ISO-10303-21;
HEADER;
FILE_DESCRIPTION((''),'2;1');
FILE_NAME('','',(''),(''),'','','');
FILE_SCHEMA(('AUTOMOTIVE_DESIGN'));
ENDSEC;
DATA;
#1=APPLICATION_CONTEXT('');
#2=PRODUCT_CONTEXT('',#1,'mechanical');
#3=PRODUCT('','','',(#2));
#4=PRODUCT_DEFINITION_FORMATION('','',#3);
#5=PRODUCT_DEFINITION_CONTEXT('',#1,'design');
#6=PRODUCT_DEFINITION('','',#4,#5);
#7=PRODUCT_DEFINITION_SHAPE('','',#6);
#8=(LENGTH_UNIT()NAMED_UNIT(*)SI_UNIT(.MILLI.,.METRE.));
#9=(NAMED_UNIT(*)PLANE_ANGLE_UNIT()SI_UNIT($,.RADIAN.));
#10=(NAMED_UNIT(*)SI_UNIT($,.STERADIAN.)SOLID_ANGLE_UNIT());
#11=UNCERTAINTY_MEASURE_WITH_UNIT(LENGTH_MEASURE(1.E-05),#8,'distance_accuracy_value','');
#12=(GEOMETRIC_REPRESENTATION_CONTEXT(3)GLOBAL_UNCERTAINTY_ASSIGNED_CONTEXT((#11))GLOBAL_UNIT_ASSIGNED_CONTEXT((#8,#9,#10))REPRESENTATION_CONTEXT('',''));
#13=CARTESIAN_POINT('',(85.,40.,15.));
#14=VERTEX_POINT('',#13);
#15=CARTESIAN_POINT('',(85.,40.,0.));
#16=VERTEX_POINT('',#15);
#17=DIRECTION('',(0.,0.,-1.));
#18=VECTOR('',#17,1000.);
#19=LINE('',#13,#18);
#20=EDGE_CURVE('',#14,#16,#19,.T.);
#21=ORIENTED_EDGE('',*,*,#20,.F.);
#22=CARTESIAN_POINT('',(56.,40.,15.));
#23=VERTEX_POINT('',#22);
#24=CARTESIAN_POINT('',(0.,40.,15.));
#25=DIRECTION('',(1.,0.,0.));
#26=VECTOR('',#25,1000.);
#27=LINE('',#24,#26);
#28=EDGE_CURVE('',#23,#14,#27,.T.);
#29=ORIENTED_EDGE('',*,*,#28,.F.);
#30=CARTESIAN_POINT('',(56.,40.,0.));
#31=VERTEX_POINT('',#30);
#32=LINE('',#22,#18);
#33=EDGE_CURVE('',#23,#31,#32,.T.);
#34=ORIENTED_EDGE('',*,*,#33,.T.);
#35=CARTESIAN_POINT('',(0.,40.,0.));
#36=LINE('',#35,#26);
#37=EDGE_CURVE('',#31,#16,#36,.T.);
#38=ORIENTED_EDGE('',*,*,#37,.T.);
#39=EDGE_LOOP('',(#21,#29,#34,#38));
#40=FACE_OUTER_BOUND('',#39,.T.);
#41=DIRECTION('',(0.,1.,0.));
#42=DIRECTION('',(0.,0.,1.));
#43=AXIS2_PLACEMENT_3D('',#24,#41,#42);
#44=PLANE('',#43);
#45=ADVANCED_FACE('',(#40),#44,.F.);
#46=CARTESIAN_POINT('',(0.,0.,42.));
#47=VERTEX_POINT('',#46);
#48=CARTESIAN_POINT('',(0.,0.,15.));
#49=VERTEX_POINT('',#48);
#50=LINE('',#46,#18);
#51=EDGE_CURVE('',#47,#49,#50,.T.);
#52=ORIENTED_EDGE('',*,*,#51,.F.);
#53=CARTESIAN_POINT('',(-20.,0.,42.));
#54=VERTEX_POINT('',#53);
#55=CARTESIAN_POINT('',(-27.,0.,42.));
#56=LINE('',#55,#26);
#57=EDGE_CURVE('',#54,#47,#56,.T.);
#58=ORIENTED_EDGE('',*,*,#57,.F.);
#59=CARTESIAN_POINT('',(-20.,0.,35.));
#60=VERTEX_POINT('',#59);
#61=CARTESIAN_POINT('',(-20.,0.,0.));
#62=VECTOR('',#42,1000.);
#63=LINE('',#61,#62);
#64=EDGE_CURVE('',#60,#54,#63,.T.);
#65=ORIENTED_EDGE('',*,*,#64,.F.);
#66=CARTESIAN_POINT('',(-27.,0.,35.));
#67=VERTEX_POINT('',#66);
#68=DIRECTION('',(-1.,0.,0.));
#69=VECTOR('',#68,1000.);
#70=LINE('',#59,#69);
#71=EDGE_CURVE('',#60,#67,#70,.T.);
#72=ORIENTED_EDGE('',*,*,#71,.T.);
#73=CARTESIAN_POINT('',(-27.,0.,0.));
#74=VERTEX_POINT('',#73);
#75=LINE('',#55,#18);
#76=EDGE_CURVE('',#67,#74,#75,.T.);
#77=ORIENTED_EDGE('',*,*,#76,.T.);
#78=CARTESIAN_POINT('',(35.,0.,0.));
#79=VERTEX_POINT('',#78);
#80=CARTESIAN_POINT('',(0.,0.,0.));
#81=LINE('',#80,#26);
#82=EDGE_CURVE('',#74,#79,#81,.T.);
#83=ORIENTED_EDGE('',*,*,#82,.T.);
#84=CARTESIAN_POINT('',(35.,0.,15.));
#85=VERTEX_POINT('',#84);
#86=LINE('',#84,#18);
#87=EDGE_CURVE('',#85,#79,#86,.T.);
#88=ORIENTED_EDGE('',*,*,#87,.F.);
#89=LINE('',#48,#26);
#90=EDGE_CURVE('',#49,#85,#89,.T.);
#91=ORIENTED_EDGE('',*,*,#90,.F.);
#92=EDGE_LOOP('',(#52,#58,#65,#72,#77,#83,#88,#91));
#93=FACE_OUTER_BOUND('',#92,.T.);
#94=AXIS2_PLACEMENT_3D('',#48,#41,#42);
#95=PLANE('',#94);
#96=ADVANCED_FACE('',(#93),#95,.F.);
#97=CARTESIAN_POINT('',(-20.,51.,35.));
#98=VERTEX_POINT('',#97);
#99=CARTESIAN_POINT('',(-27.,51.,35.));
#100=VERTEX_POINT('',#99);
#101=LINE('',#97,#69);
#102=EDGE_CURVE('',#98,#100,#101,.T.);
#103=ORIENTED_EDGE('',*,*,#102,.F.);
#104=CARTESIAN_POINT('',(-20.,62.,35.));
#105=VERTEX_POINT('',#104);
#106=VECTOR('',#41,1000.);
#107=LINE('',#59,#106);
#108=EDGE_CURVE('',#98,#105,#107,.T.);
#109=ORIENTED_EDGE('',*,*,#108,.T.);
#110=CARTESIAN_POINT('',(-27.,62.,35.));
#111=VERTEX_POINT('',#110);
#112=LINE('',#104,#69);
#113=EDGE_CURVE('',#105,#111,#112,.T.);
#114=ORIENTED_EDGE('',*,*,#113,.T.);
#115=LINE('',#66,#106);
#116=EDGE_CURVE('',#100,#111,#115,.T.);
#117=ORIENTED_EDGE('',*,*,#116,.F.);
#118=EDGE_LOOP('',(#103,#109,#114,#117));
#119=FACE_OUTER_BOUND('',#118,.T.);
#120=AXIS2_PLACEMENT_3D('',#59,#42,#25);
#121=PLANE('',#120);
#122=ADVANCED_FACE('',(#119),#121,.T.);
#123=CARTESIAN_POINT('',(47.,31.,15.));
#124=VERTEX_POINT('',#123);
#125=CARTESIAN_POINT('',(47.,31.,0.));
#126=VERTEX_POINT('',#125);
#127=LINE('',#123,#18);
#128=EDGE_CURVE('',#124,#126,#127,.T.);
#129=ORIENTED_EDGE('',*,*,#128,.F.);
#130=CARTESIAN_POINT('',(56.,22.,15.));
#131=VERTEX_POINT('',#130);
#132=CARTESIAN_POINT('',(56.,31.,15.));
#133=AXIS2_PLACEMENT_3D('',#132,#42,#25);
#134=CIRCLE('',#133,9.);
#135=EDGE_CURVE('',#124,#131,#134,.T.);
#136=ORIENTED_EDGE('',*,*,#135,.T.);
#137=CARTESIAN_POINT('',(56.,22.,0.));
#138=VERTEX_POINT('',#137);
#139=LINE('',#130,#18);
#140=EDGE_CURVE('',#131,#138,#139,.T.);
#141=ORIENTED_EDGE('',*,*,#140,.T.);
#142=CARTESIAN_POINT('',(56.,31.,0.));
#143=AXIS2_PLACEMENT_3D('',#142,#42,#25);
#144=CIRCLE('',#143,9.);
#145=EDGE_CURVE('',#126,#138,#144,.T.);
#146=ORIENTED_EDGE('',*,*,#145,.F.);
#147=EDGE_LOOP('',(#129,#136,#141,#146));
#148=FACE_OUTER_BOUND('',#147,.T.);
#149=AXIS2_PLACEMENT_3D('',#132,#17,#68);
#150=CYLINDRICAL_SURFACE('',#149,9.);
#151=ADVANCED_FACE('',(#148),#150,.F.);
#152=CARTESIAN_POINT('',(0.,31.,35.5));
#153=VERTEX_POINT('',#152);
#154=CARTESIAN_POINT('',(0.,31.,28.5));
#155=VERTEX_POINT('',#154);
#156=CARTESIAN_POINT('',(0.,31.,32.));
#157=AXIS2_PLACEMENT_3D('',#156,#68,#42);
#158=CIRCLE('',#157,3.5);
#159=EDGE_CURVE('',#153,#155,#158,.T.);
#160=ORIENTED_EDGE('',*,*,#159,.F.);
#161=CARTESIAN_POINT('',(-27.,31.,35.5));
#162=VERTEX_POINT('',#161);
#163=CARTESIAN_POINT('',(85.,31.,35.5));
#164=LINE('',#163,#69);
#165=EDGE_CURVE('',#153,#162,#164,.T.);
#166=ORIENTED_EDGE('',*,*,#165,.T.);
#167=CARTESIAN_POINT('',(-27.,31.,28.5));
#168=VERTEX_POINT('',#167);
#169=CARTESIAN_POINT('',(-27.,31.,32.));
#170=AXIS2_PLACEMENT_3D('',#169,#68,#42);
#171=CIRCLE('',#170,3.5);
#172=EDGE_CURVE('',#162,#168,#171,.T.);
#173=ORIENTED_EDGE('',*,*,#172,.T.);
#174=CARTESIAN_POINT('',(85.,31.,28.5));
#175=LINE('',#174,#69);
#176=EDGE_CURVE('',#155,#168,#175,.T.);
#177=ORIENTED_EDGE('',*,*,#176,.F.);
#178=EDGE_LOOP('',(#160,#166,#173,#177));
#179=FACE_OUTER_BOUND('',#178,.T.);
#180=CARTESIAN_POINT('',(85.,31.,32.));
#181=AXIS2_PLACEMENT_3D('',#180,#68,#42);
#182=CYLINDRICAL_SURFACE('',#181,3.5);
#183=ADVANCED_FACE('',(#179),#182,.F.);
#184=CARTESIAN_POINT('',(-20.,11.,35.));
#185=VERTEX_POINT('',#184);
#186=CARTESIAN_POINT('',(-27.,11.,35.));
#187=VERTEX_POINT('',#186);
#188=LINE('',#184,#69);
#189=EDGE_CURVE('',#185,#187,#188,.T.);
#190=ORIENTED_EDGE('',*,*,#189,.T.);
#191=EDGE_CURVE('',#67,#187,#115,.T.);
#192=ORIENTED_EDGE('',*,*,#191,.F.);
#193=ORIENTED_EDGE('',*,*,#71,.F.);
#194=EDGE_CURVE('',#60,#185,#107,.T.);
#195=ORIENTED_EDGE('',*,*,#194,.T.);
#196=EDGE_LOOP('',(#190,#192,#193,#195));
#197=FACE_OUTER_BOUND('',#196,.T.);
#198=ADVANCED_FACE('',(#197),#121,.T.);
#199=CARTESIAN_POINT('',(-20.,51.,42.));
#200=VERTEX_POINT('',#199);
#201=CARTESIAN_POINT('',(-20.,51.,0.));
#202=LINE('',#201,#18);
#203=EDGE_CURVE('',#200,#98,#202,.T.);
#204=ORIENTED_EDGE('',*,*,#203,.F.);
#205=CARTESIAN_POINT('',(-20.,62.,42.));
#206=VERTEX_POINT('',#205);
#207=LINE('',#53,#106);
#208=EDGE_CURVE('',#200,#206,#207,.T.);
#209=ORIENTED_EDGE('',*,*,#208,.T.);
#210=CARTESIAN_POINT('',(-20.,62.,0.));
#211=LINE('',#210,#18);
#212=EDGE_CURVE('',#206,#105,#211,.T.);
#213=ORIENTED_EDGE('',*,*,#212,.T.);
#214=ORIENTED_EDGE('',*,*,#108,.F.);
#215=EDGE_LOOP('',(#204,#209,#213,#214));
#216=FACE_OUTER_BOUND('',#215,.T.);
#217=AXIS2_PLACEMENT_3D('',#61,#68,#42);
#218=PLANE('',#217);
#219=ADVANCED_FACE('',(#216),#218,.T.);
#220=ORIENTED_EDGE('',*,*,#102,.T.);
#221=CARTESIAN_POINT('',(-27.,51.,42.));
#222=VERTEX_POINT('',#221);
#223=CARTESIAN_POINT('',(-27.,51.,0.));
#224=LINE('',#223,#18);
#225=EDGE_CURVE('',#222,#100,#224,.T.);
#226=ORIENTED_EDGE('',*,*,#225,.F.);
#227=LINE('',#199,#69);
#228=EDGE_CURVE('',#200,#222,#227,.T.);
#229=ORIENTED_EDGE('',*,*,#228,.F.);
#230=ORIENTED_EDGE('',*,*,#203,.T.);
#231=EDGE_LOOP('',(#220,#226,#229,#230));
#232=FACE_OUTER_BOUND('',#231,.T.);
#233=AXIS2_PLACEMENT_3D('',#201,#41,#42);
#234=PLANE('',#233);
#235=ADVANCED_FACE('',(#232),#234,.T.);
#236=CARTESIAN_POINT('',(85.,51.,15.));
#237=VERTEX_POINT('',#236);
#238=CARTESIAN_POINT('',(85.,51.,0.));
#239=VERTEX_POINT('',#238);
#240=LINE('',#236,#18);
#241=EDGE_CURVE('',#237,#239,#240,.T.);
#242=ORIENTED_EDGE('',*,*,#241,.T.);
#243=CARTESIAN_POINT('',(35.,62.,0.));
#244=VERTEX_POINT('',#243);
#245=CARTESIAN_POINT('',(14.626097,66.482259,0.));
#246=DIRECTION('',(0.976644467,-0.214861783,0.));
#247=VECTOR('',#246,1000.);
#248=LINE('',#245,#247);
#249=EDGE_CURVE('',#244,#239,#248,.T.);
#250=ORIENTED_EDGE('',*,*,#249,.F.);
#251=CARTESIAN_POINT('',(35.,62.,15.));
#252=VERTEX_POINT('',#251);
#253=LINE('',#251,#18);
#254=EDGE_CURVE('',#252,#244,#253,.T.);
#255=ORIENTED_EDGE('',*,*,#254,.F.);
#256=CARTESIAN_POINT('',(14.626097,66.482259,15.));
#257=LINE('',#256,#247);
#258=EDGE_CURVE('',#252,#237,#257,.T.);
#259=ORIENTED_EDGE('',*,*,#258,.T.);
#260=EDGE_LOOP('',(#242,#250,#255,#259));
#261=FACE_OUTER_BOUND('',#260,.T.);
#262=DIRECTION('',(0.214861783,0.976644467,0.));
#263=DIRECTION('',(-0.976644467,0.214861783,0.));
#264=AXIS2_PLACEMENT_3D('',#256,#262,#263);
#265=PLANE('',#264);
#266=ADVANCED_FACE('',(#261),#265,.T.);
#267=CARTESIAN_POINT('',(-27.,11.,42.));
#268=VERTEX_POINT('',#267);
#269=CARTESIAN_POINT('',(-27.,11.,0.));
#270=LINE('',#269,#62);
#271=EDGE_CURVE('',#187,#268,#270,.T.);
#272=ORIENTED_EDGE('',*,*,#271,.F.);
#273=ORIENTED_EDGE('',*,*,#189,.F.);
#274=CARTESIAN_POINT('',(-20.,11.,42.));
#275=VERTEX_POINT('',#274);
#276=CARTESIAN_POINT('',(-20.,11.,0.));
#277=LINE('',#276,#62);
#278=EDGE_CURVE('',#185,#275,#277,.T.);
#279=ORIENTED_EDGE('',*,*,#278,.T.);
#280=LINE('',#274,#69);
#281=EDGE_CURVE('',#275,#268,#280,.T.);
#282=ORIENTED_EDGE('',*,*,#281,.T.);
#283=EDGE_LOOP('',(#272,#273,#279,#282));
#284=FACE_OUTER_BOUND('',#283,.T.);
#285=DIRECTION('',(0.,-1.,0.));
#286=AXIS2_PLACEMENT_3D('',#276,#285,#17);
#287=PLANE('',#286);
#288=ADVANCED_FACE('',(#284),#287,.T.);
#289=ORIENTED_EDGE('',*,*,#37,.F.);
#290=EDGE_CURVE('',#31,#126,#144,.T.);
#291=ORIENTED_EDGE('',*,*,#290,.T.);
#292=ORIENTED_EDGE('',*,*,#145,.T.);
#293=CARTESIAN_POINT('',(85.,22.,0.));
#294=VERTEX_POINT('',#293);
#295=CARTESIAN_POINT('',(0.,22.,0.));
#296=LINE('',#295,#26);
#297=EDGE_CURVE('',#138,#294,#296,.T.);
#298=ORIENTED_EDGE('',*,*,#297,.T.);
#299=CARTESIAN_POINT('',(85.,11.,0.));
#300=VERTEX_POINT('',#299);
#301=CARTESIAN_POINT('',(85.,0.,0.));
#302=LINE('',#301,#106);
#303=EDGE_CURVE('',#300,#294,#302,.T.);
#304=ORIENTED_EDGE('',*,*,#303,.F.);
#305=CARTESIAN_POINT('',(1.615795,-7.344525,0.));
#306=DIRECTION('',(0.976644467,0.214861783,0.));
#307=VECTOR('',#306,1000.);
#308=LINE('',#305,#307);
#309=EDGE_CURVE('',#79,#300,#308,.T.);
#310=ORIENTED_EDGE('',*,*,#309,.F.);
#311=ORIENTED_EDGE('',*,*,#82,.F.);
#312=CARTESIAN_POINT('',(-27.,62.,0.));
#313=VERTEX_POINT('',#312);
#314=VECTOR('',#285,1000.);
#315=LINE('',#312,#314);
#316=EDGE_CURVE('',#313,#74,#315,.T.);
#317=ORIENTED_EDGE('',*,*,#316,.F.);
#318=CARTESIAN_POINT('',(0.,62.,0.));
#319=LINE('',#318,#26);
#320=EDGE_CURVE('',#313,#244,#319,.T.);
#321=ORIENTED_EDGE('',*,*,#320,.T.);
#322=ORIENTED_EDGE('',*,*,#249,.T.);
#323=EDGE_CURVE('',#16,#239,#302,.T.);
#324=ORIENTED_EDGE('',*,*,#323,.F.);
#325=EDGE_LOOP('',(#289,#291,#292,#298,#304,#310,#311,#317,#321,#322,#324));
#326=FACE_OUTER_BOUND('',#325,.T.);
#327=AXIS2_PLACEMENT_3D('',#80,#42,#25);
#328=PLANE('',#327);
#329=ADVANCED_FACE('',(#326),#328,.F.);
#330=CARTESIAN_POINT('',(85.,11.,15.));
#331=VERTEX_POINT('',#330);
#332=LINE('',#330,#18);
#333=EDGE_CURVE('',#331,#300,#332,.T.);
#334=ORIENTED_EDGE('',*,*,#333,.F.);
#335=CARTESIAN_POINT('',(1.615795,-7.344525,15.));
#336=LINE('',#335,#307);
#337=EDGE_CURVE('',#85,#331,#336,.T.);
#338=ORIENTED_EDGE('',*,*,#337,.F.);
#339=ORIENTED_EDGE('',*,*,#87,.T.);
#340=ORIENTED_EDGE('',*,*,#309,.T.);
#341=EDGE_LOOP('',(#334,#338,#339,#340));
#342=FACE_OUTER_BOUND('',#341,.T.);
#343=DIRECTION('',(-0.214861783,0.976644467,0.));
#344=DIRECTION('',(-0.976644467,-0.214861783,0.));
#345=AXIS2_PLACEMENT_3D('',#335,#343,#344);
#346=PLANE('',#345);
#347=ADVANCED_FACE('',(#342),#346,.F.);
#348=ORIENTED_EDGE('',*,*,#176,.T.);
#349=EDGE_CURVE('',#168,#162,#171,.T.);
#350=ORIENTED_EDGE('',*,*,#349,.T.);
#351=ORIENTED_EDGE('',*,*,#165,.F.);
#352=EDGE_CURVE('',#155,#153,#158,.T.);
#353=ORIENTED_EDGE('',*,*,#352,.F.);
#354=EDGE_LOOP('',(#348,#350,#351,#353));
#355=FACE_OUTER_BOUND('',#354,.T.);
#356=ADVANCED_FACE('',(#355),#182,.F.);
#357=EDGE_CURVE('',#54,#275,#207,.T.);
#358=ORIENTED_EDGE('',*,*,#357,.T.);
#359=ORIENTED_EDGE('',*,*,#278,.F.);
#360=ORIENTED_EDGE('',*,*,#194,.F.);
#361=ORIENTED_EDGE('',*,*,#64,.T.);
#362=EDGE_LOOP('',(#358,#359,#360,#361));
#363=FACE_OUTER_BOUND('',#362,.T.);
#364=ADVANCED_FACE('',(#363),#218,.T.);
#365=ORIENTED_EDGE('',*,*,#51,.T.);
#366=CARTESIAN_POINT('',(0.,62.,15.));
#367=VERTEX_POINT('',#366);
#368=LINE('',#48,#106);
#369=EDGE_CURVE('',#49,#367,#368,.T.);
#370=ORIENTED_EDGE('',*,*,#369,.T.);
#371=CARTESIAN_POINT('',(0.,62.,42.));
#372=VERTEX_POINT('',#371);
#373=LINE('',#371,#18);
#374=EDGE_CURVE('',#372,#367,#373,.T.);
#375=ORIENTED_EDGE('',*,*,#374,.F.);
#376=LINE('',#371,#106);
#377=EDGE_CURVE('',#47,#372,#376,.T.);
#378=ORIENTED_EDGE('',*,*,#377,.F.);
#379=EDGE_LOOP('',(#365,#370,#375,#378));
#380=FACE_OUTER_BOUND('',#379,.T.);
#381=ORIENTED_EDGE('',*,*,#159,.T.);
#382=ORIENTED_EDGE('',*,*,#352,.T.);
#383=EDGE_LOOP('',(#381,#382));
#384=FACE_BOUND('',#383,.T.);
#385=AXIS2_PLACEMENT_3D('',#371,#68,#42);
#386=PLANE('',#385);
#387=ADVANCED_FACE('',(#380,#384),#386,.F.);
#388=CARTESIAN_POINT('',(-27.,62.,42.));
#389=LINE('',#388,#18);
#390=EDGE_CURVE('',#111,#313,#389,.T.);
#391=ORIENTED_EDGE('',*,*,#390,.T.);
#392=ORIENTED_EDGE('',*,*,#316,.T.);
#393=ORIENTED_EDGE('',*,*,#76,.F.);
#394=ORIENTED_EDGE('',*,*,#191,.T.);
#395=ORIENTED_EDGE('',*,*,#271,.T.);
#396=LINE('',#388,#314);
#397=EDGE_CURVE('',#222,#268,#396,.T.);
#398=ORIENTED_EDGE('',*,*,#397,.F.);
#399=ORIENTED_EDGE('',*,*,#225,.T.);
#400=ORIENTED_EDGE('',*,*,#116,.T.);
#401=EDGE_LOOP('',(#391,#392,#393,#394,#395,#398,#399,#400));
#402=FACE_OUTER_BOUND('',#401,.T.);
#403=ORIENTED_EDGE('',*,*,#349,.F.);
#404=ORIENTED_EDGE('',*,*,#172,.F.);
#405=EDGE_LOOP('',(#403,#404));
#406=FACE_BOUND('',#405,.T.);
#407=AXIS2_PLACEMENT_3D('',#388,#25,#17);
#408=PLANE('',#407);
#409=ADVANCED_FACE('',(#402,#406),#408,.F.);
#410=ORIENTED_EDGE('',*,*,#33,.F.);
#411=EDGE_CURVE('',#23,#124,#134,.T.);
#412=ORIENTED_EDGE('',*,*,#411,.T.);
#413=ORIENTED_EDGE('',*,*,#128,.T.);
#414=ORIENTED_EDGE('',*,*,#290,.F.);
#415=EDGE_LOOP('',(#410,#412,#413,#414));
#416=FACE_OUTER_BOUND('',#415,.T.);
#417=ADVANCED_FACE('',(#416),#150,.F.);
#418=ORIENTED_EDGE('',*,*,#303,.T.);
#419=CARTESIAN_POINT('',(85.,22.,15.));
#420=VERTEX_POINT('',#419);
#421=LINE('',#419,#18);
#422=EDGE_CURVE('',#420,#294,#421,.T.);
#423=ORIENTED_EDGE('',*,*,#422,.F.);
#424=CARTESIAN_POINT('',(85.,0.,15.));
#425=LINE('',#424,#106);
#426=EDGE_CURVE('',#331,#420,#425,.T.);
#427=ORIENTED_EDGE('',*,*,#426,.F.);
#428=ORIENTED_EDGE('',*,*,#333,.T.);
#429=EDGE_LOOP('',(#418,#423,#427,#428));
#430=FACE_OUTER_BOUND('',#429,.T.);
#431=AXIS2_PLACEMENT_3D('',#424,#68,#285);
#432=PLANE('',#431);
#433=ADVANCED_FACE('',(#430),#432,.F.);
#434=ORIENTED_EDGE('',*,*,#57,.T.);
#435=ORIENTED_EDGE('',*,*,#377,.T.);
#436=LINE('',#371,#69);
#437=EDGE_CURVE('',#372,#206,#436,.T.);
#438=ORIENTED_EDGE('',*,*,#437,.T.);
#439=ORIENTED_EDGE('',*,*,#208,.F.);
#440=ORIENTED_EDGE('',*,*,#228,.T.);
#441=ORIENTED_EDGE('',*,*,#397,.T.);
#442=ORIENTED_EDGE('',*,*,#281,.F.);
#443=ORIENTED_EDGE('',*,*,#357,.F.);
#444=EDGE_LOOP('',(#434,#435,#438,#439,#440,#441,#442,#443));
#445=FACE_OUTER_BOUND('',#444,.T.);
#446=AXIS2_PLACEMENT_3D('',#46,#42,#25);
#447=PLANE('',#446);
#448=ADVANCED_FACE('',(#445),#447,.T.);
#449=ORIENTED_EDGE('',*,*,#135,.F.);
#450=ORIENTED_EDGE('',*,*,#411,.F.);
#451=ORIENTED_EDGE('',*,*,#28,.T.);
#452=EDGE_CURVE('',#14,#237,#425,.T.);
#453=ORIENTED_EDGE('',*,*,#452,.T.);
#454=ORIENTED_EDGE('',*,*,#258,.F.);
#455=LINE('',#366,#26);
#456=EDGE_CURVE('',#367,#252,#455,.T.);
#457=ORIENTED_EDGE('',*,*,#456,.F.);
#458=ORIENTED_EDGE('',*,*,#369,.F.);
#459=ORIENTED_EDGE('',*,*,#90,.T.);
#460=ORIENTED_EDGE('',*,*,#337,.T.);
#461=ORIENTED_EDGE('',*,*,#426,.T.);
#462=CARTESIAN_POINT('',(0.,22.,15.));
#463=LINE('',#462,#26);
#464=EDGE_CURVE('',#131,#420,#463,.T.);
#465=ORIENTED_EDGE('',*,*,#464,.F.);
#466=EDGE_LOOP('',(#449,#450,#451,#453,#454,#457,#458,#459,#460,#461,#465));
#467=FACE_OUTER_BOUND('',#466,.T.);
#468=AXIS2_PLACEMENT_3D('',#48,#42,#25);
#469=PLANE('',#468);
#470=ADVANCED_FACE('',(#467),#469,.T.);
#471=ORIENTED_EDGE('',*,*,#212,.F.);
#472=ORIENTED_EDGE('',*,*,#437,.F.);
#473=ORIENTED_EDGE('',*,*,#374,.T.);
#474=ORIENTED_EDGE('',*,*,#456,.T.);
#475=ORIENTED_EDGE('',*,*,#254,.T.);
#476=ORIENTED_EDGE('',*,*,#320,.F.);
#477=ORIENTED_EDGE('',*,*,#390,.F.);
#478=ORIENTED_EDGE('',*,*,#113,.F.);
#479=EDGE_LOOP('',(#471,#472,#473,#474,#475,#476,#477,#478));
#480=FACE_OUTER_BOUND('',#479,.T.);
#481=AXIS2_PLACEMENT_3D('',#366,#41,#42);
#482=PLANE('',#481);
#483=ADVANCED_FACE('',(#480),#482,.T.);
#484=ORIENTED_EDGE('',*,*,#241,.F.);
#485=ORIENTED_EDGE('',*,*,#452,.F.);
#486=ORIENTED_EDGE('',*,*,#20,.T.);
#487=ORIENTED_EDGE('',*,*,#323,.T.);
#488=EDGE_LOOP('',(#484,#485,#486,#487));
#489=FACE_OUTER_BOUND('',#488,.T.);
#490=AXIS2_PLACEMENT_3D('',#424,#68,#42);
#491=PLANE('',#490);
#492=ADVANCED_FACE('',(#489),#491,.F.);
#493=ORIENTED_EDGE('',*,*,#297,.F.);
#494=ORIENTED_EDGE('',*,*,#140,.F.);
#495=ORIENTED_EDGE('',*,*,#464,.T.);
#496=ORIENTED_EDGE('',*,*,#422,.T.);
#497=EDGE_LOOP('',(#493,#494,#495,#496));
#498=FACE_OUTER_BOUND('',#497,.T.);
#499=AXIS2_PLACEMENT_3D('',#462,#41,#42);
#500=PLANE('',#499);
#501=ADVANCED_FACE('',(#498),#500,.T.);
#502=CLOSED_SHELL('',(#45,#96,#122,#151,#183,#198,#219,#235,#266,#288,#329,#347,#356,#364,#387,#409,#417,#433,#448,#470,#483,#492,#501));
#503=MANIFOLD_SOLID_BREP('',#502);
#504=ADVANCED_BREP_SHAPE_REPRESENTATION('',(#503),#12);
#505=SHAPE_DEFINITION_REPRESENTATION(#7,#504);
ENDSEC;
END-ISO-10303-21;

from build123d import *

# Parameters (mm, degrees)
FORK_ARM_PLATE_DEPTH    = 15
MOUNTING_BLOCK_SKETCH_W = 27
MOUNTING_BLOCK_SKETCH_H = 62
MOUNTING_BLOCK_DEPTH    = 42
BLOCK_STEP_CUT_SKETCH_W = 7
BLOCK_STEP_CUT_SKETCH_H = 11
BLOCK_STEP_CUT_DEPTH    = 7
SIDE_HOLE_7_SKETCH_R    = 3.5
SIDE_HOLE_7_DEPTH       = 135.729358345


with BuildPart() as part:
    # Fork Arm Profile Sketch → Fork Arm Plate (new body)
    with BuildSketch(Plane.XY):
        with BuildLine():
            ThreePointArc((56, 40), (47, 31), (56, 22))
            Line((56, 22), (85, 22))
            Line((85, 22), (85, 11))
            Line((85, 11), (35, 0))
            Line((35, 0), (0, 0))
            Line((0, 0), (0, 62))
            Line((0, 62), (35, 62))
            Line((35, 62), (85, 51))
            Line((85, 51), (85, 40))
            Line((85, 40), (56, 40))
        make_face()
    extrude(amount=FORK_ARM_PLATE_DEPTH)

    # Mounting Block Sketch → Mounting Block (add)
    with BuildSketch(Plane.XY):
        with Locations((-13.5, 31)):
            Rectangle(MOUNTING_BLOCK_SKETCH_W, MOUNTING_BLOCK_SKETCH_H)
    extrude(amount=MOUNTING_BLOCK_DEPTH)

    # Block Step Cut Sketch → Block Step Cut (cut)
    with BuildSketch(Plane.ZY.offset(27)):
        with Locations((38.5, 56.5)):
            Rectangle(BLOCK_STEP_CUT_SKETCH_W, BLOCK_STEP_CUT_SKETCH_H)
        with Locations((38.5, 5.5)):
            Rectangle(BLOCK_STEP_CUT_SKETCH_W, BLOCK_STEP_CUT_SKETCH_H)
    extrude(amount=-BLOCK_STEP_CUT_DEPTH, mode=Mode.SUBTRACT)

    # Side Hole Ø7 Sketch → Side Hole Ø7 (cut, through all)
    with BuildSketch(Plane.ZY.offset(27)):
        with Locations((32, 31)):
            Circle(SIDE_HOLE_7_SKETCH_R)
    extrude(amount=-SIDE_HOLE_7_DEPTH, mode=Mode.SUBTRACT)


solid = part.part
